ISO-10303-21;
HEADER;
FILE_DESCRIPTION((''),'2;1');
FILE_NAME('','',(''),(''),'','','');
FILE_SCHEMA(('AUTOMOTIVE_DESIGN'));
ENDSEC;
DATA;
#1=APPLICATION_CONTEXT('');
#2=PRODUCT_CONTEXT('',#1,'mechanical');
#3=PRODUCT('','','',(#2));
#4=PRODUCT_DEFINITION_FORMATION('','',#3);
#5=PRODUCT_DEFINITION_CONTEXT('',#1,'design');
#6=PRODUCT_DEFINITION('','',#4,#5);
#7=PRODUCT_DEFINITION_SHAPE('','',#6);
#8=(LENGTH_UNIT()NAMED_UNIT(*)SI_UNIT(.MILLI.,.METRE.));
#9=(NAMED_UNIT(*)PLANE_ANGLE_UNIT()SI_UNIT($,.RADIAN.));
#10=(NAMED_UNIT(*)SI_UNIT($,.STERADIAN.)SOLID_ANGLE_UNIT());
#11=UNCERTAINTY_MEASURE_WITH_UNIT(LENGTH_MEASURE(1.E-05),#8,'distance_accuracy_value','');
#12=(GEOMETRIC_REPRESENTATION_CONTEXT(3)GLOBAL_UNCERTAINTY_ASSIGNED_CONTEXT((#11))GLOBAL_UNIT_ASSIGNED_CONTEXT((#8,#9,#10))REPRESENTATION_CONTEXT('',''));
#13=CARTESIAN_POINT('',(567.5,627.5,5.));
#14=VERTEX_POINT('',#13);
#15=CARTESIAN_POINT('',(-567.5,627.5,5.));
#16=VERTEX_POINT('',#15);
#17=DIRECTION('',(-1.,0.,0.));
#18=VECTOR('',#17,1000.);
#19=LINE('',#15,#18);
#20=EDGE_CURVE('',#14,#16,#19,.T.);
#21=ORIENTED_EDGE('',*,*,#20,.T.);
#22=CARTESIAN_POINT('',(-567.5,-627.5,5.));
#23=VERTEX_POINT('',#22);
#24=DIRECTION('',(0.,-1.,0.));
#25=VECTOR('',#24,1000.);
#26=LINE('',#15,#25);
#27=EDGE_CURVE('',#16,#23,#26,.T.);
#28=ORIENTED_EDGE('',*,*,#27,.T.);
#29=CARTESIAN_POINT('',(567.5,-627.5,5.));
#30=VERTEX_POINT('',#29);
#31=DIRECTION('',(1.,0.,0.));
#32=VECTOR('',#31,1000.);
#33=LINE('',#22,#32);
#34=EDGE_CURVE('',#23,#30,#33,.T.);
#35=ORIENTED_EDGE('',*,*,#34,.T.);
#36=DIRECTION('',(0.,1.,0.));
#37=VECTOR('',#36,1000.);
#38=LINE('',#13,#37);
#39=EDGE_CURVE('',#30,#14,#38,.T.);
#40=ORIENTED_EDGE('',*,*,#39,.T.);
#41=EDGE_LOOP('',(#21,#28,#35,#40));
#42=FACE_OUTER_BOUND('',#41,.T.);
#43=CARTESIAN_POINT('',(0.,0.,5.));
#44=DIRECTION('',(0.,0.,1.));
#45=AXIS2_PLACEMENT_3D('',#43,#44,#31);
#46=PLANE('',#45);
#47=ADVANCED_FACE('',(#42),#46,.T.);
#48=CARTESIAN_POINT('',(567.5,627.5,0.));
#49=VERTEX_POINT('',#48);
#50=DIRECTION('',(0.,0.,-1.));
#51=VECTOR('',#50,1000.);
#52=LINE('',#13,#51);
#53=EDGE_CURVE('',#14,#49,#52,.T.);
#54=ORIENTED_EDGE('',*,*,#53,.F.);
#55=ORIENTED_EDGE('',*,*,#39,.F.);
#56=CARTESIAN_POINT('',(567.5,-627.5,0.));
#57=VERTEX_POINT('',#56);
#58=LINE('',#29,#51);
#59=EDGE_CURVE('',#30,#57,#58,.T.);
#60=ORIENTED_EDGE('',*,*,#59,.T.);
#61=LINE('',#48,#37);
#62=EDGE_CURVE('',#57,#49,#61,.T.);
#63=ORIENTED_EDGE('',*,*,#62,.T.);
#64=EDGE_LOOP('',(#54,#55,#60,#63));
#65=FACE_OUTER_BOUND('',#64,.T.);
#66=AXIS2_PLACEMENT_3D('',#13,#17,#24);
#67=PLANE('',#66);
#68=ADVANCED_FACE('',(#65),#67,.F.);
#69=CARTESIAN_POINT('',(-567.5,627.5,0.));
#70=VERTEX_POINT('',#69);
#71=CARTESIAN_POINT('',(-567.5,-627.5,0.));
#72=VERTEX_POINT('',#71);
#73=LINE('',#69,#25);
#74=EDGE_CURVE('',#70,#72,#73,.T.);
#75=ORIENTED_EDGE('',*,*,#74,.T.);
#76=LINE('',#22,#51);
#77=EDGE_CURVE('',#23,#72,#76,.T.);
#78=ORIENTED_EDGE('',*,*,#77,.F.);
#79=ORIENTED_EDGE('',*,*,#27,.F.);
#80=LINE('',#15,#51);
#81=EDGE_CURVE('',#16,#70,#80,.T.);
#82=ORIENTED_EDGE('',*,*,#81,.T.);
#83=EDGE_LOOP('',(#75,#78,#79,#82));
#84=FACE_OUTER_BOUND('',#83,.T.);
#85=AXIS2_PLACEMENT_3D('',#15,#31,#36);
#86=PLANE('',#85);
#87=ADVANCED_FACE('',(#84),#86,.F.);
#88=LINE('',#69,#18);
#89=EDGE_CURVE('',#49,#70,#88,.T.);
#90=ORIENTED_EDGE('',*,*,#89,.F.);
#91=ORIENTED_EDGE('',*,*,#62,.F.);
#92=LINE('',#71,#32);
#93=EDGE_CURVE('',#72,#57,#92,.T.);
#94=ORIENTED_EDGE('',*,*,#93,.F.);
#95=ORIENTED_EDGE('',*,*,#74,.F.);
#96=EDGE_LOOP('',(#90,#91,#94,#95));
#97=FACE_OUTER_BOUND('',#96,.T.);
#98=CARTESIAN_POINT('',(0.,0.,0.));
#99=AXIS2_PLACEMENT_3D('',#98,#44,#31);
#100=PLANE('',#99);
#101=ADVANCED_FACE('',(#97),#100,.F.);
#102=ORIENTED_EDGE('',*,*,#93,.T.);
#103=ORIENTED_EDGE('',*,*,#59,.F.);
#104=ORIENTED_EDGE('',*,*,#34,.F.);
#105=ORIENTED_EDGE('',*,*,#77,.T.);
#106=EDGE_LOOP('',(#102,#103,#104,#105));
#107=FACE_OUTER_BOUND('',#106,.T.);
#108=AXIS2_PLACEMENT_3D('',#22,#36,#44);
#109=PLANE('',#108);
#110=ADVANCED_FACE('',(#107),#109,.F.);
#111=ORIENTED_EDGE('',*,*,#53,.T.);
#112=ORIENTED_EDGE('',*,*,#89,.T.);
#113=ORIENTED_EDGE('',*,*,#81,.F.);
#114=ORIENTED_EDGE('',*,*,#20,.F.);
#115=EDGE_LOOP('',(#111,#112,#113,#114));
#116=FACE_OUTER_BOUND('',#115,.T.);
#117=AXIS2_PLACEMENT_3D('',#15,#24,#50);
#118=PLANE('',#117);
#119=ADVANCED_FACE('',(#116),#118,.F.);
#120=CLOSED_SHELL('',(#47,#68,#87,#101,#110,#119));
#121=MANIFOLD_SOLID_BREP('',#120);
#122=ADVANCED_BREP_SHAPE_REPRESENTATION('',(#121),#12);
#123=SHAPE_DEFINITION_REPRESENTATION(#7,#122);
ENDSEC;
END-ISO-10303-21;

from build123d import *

# Parameters (mm, degrees)
SKETCH_1_W      = 1135
SKETCH_1_H      = 1255
EXTRUDE_1_DEPTH = 5


with BuildPart() as part:
    # 草图1 → 凸台-拉伸1 (new body)
    with BuildSketch(Plane.XY):
        Rectangle(SKETCH_1_W, SKETCH_1_H)
    extrude(amount=EXTRUDE_1_DEPTH)


solid = part.part
